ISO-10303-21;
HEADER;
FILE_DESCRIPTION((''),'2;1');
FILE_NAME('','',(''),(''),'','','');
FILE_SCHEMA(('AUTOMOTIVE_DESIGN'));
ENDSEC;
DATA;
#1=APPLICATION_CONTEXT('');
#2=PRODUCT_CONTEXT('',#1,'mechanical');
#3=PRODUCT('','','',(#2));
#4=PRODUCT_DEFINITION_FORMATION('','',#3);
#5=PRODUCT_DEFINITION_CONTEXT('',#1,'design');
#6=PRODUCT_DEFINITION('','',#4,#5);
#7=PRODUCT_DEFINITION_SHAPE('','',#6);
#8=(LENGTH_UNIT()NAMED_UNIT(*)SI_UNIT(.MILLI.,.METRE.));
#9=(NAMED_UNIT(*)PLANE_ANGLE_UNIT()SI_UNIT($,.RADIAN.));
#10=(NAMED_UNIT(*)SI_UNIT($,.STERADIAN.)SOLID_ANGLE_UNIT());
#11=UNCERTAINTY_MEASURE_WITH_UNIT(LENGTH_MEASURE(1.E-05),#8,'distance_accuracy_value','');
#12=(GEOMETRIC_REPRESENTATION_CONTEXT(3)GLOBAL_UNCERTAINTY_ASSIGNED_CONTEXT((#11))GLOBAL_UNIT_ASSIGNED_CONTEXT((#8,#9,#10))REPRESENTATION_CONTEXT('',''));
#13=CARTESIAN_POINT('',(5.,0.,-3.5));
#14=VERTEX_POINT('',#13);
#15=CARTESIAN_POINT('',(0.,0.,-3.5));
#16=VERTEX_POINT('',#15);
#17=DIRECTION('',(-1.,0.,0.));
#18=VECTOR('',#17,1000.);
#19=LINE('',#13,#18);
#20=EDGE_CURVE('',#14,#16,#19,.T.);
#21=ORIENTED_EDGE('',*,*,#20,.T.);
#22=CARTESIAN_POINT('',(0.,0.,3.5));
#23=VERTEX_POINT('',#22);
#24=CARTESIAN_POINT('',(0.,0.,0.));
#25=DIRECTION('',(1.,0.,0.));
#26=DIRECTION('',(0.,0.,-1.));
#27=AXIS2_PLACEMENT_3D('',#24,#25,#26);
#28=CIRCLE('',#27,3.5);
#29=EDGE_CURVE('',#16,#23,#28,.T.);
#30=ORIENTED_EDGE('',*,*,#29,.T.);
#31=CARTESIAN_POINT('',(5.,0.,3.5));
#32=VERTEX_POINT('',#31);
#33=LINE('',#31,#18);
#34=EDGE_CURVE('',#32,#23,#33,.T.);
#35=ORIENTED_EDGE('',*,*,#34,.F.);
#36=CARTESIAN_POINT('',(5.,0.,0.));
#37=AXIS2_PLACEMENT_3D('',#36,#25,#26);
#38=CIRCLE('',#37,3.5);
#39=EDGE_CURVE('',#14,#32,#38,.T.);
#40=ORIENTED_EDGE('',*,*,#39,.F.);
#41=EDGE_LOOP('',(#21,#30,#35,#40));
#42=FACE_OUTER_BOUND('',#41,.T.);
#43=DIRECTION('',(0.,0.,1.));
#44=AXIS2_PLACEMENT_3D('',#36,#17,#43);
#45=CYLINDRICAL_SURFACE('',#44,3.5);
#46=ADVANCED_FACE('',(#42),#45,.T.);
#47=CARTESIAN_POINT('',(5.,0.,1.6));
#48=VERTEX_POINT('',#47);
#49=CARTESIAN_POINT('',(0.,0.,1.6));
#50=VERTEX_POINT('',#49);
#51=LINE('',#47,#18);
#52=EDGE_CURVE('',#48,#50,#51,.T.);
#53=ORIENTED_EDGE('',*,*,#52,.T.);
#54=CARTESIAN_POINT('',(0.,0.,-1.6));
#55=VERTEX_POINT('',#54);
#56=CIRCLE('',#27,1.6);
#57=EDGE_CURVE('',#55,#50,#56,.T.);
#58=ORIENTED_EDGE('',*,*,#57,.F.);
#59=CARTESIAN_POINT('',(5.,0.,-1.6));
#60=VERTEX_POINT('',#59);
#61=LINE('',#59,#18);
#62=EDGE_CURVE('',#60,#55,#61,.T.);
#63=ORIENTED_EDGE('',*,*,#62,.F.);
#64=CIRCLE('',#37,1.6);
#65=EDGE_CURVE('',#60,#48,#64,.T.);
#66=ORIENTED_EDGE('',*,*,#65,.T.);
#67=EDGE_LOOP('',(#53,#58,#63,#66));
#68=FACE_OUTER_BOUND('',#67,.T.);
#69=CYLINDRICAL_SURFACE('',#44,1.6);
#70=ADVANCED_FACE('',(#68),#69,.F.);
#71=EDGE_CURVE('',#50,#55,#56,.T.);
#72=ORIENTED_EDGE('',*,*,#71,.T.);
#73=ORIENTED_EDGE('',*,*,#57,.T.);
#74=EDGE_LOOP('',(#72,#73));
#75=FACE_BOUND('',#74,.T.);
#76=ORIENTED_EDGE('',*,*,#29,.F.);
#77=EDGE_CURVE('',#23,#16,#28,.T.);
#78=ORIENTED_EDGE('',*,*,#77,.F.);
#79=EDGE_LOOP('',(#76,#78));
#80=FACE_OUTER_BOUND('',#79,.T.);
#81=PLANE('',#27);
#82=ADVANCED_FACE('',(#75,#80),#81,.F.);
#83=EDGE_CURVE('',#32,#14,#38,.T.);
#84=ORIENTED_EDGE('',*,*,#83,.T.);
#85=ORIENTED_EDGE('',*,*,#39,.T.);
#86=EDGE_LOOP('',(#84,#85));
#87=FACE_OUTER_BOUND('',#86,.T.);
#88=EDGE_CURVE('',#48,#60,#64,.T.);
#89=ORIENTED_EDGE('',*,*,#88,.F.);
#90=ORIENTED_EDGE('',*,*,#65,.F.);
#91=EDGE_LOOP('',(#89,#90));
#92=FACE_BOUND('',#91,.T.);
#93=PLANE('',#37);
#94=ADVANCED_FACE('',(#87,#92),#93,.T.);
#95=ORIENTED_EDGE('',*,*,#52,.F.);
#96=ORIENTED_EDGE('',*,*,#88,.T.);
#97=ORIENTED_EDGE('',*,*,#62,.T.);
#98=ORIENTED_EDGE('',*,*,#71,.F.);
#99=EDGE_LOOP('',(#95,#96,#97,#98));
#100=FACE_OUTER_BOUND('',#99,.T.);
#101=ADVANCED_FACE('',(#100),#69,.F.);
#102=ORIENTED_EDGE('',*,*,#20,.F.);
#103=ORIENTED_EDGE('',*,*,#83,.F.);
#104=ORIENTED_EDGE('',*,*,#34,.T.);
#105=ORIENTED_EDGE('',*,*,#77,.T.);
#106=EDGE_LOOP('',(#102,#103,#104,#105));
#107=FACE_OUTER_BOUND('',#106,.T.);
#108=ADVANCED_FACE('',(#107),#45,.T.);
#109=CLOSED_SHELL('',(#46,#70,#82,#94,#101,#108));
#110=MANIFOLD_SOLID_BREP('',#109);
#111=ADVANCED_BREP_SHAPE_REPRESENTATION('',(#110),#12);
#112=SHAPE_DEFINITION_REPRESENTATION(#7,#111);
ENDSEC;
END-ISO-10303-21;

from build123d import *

# Parameters (mm, degrees)
SKETCH_1_R      = 3.5
SKETCH_1_R_2    = 1.6
EXTRUDE_1_DEPTH = 5


with BuildPart() as part:
    # 草图1 → 凸台-拉伸1 (new body)
    with BuildSketch(Plane(origin=(0, 0, 0), x_dir=(0, 0, -1), z_dir=(1, 0, 0))):
        Circle(SKETCH_1_R)
        Circle(SKETCH_1_R_2, mode=Mode.SUBTRACT)
    extrude(amount=EXTRUDE_1_DEPTH)


solid = part.part
